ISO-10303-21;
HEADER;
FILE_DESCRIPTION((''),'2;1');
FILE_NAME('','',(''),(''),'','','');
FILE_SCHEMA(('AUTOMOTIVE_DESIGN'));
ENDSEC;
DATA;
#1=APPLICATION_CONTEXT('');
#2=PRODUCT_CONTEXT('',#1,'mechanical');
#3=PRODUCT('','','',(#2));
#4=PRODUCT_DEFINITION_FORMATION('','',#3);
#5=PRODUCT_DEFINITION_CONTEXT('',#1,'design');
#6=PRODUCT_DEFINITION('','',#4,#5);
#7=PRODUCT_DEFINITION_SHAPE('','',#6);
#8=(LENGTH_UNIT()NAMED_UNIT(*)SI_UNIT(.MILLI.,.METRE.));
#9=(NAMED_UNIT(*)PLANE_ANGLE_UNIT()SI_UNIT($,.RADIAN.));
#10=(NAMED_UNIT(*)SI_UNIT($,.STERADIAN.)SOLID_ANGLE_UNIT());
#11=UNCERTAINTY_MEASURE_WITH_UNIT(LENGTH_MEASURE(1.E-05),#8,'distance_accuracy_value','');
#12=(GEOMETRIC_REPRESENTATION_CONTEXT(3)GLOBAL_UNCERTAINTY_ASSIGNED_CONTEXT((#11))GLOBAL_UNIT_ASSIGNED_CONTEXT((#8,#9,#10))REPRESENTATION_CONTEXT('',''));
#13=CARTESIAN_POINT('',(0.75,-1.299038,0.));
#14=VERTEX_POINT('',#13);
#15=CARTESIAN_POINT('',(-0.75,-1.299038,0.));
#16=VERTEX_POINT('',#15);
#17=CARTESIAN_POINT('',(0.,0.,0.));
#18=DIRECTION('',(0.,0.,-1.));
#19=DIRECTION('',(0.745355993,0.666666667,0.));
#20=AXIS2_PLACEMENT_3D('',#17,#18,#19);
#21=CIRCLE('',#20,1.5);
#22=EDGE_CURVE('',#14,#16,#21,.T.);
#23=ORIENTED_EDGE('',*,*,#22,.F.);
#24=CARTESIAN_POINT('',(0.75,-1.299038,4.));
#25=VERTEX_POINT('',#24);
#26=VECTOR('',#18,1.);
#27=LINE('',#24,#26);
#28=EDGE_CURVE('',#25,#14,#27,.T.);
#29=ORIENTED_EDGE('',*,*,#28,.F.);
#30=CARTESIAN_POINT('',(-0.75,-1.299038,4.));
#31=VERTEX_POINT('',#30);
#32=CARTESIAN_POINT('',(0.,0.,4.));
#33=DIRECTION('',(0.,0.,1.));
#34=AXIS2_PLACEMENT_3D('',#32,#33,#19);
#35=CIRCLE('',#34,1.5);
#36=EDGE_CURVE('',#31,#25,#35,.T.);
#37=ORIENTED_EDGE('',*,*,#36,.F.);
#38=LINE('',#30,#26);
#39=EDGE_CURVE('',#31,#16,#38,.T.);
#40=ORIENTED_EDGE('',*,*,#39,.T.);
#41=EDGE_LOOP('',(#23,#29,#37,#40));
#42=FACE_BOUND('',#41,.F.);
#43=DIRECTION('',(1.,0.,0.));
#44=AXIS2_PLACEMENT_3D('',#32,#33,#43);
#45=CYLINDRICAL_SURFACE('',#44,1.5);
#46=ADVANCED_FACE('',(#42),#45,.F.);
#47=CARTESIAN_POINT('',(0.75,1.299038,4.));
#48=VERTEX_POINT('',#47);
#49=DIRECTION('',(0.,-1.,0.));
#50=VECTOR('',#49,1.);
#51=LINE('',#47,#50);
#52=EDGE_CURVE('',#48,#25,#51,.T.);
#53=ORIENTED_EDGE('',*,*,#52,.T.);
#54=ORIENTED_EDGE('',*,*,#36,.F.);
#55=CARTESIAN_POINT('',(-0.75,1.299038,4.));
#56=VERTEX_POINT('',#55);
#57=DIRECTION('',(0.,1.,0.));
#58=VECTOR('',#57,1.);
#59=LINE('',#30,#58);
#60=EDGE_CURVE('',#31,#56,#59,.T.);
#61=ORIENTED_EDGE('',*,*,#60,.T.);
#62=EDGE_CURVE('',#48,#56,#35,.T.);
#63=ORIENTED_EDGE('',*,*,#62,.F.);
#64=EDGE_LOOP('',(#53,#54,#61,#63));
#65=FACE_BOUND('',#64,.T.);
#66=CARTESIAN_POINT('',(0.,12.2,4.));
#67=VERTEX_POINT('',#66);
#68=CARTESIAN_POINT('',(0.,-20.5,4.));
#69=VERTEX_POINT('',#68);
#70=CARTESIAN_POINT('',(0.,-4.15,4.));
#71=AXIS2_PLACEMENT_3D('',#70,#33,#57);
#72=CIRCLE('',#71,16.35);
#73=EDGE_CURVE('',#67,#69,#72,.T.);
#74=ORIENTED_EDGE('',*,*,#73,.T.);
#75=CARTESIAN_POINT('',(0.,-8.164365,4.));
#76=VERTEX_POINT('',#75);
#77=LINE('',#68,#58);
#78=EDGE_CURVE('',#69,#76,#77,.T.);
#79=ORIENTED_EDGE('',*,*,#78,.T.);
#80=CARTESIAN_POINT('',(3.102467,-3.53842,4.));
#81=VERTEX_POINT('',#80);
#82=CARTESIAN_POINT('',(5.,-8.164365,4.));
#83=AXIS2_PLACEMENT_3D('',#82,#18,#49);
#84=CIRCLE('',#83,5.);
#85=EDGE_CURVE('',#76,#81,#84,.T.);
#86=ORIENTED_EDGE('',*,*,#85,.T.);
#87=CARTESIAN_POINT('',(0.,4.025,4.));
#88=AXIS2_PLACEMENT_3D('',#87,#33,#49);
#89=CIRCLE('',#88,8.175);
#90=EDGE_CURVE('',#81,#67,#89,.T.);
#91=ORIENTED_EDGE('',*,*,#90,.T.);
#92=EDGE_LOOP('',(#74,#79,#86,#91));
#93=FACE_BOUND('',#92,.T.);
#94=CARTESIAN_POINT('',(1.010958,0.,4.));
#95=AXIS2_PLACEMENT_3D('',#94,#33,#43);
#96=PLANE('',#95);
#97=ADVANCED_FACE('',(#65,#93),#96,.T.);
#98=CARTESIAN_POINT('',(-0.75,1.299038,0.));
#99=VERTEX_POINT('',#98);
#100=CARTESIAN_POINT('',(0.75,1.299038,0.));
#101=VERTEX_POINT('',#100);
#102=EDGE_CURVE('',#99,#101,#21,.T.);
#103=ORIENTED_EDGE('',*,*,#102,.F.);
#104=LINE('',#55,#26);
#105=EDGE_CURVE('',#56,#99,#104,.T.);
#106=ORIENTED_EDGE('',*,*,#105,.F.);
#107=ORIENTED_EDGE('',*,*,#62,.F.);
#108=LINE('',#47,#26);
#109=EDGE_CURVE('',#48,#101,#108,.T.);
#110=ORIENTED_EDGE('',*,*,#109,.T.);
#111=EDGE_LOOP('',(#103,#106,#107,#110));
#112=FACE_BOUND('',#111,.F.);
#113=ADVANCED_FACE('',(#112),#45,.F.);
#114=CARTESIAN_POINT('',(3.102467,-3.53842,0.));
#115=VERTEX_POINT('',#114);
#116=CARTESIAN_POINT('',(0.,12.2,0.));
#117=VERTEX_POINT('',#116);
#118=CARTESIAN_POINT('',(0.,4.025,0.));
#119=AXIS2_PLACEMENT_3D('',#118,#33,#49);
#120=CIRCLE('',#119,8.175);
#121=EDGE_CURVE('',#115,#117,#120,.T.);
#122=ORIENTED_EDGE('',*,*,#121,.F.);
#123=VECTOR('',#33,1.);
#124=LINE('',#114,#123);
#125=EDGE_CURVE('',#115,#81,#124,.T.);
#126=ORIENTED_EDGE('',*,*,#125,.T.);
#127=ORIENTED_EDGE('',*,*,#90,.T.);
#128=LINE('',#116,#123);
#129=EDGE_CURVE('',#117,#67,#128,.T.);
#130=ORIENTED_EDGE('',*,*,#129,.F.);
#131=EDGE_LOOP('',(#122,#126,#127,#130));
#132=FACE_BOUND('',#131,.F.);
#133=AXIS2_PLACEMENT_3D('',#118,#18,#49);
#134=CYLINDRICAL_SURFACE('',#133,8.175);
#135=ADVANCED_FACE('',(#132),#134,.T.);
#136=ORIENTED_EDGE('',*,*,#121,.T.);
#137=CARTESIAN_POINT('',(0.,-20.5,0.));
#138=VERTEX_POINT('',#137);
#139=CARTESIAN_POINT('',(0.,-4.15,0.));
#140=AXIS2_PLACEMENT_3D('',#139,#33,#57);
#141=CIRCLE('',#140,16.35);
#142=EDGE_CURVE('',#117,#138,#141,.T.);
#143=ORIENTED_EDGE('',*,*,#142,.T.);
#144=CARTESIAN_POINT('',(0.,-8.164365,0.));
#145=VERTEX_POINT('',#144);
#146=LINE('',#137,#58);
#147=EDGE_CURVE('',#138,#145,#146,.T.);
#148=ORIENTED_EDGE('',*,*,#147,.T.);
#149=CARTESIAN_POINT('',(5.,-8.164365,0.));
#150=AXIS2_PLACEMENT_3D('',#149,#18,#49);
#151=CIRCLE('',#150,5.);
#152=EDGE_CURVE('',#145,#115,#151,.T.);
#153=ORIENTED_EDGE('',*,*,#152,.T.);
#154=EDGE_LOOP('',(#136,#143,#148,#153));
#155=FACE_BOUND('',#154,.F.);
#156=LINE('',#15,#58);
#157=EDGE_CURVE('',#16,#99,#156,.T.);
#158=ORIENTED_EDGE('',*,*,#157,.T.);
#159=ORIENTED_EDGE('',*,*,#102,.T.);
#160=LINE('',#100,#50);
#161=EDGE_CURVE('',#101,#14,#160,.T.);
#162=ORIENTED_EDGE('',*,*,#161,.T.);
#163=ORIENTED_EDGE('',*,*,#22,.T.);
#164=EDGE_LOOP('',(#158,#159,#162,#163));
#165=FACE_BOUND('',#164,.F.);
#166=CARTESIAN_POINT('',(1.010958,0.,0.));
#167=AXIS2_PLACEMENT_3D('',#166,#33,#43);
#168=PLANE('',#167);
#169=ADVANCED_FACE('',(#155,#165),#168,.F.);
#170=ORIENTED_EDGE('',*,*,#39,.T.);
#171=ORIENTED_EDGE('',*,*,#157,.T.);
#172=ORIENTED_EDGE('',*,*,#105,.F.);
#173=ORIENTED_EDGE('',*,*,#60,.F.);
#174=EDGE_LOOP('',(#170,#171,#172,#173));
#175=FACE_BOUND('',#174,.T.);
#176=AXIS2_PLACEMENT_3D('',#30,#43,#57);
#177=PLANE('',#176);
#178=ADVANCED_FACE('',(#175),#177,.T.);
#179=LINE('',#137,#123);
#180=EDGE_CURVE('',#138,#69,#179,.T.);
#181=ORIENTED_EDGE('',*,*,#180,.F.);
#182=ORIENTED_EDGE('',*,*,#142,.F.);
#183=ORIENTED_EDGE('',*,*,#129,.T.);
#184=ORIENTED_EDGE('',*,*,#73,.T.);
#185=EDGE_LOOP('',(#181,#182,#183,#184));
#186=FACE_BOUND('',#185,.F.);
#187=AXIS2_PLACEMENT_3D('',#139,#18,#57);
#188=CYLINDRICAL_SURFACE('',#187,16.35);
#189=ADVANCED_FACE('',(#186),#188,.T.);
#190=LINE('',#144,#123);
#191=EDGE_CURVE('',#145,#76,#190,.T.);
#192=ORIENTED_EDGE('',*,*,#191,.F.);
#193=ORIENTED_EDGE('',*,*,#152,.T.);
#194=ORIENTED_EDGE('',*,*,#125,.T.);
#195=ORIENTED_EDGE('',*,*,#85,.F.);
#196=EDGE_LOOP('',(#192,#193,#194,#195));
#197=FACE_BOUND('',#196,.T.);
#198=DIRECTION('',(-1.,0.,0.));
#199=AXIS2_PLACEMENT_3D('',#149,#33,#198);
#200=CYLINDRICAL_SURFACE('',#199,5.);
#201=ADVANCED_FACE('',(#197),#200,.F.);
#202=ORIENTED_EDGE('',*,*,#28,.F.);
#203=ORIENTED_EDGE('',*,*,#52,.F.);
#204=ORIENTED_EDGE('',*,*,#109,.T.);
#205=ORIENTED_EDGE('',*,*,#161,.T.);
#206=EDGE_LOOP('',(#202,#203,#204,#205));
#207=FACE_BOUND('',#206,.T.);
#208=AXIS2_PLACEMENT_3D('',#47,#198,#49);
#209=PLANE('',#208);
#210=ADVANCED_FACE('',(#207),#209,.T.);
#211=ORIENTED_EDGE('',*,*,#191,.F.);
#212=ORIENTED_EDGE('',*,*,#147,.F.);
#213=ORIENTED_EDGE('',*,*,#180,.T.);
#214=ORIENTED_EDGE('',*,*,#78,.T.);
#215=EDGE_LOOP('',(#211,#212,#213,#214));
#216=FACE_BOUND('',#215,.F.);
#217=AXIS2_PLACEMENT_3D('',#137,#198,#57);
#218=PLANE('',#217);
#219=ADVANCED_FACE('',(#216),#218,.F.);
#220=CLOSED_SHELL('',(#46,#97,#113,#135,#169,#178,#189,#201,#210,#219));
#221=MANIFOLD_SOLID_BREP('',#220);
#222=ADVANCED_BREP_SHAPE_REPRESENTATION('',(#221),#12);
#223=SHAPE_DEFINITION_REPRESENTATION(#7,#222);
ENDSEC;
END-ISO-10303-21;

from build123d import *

# Parameters (mm, degrees)
SKETCH4_R           = 2.5
BOSS_EXTRUDE3_DEPTH = 4
FILLET2_R           = 5
SKETCH7_R           = 3.986171954
SKETCH7_R_2         = 1.5
BOSS_EXTRUDE4_DEPTH = 4
BOSS_EXTRUDE5_DEPTH = 4
SKETCH9_R           = 1.5
CUT_EXTRUDE1_DEPTH  = 27.524941093
BOSS_EXTRUDE6_DEPTH = 4


with BuildPart() as part:
    # Sketch4 → Boss-Extrude3 (new body)
    with BuildSketch(Plane.XY):
        with BuildLine():
            Line((0, -20.5), (0, -4.15))
            ThreePointArc((0, -4.15), (8.175, 4.025), (0, 12.2))
            ThreePointArc((0, 12.2), (-16.35, -4.15), (0, -20.5))
        make_face()
        Circle(SKETCH4_R, mode=Mode.SUBTRACT)
    extrude(amount=BOSS_EXTRUDE3_DEPTH)

    # Fillet2
    fillet2_edges = [part.edges().sort_by_distance(p)[0] for p in [
        (0, -4.15, 2),
    ]]
    fillet(fillet2_edges, radius=FILLET2_R)

    # Sketch7 → Boss-Extrude4 (add)
    with BuildSketch(Plane.XY.offset(4)):
        Circle(SKETCH7_R)
        Circle(SKETCH7_R_2, mode=Mode.SUBTRACT)
    extrude(amount=-BOSS_EXTRUDE4_DEPTH)

    # Sketch8 → Boss-Extrude5 (add)
    with BuildSketch(Plane.XY.offset(4)):
        Polygon((0, 0), (-1, 1.118033989), (-1.075164003, 1.990831029), (0.996128458, 2.028687549), (1.118033989, 1), align=None)
    extrude(amount=-BOSS_EXTRUDE5_DEPTH)

    # Sketch9 → Cut-Extrude1 (cut, through all)
    with BuildSketch(Plane.XY.offset(4)):
        Circle(SKETCH9_R)
    extrude(amount=-CUT_EXTRUDE1_DEPTH, mode=Mode.SUBTRACT)

    # Sketch10 → Boss-Extrude6 (add, through all)
    with BuildSketch(Plane.XY.offset(4)):
        with BuildLine():
            ThreePointArc((1.5, 0), (1.299038106, 0.75), (0.75, 1.299038106))
            Line((0.75, 1.299038106), (0.75, -1.299038106))
            ThreePointArc((0.75, -1.299038106), (1.299038106, -0.75), (1.5, 0))
        make_face()
        with BuildLine():
            Line((-0.75, -1.299038106), (-0.75, 1.299038106))
            ThreePointArc((-0.75, 1.299038106), (-1.5, 0), (-0.75, -1.299038106))
        make_face()
    extrude(amount=-BOSS_EXTRUDE6_DEPTH)


solid = part.part
